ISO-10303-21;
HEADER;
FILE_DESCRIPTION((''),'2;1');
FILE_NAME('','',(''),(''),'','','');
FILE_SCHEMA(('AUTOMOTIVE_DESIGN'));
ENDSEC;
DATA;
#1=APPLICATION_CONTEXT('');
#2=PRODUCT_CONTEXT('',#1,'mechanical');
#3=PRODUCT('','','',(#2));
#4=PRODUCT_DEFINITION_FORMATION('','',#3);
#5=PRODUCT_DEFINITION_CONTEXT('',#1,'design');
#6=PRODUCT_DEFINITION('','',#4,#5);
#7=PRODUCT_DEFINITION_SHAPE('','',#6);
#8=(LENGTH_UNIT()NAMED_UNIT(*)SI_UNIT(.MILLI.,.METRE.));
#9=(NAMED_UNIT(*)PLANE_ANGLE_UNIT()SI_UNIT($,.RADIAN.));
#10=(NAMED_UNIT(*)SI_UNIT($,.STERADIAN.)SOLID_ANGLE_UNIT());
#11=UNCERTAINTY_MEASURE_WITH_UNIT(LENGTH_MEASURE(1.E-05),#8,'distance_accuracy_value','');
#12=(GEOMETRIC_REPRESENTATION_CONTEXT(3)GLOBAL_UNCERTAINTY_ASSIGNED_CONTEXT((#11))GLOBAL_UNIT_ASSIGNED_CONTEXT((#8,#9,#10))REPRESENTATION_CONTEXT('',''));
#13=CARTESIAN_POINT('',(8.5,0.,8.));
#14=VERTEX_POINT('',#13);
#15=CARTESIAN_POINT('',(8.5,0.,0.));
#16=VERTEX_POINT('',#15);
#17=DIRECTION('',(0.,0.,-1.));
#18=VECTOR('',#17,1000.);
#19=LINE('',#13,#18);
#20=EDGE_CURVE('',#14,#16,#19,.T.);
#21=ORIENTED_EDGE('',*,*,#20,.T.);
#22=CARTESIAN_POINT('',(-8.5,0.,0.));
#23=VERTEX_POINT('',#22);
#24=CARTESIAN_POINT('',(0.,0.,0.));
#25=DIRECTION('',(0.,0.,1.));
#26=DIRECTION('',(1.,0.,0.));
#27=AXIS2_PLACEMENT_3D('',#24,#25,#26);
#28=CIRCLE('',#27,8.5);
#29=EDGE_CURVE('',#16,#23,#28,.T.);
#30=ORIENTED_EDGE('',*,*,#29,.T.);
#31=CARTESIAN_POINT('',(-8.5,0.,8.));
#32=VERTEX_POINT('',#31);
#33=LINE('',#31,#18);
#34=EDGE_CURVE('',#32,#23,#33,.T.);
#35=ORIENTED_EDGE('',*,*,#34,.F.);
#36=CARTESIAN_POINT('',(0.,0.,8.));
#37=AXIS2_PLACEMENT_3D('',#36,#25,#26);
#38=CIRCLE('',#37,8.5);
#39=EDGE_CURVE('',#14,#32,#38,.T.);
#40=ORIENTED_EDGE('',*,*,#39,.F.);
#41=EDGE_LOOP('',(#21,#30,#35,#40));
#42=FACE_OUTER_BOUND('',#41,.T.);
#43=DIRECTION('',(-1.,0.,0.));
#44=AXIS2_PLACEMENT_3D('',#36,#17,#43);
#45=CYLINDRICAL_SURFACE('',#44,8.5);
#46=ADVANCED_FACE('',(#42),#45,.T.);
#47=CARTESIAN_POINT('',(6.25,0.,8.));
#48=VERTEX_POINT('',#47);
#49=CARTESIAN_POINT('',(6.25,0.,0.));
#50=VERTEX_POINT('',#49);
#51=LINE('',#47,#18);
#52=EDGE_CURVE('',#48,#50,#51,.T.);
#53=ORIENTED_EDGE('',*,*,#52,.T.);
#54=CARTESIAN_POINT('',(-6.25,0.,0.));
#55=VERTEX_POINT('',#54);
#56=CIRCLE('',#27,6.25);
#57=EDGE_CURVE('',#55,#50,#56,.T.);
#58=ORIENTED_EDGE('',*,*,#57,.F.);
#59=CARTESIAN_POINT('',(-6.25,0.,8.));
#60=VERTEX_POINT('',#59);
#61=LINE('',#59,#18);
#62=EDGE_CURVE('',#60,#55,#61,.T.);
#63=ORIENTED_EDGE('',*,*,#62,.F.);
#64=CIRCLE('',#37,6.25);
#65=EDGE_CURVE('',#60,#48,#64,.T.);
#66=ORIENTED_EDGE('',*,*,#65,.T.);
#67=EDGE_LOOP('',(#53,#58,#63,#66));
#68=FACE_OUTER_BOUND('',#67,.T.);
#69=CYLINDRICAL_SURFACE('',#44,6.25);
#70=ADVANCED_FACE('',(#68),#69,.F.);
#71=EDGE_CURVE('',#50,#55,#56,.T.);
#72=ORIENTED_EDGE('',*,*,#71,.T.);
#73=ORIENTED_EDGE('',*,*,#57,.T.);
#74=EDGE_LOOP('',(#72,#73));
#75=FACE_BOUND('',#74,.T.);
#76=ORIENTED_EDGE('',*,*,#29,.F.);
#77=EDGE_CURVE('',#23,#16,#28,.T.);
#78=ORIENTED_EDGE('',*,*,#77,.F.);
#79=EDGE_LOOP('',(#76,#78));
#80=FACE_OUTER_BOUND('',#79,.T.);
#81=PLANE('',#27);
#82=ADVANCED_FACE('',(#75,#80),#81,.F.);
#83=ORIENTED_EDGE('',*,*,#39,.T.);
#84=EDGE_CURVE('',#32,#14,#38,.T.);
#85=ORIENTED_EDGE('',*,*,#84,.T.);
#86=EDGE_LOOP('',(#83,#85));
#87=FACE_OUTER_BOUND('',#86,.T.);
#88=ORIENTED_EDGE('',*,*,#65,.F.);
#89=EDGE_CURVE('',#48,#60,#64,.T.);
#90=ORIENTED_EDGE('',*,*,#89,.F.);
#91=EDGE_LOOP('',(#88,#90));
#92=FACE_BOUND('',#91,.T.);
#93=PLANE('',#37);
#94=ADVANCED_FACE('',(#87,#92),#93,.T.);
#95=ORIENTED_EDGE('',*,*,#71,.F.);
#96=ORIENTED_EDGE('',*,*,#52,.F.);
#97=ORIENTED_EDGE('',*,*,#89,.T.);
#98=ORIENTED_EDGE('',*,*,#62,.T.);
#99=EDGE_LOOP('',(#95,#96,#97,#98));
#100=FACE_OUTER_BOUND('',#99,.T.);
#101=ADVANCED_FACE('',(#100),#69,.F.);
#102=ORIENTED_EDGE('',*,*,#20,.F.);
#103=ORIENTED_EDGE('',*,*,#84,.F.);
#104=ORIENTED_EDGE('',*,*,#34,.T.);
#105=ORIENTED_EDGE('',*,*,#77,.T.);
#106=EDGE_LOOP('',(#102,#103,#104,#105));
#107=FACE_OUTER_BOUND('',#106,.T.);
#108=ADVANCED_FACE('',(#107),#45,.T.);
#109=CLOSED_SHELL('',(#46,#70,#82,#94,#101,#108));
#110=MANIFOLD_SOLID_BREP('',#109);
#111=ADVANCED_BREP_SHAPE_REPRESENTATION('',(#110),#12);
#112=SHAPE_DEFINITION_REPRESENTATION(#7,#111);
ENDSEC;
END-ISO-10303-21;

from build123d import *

# Parameters (mm, degrees)
SKETCH1_R           = 8.5
SKETCH1_R_2         = 6.25
BOSS_EXTRUDE1_DEPTH = 8


with BuildPart() as part:
    # Sketch1 → Boss-Extrude1 (new body)
    with BuildSketch(Plane.XY):
        Circle(SKETCH1_R)
        Circle(SKETCH1_R_2, mode=Mode.SUBTRACT)
    extrude(amount=BOSS_EXTRUDE1_DEPTH)


solid = part.part
